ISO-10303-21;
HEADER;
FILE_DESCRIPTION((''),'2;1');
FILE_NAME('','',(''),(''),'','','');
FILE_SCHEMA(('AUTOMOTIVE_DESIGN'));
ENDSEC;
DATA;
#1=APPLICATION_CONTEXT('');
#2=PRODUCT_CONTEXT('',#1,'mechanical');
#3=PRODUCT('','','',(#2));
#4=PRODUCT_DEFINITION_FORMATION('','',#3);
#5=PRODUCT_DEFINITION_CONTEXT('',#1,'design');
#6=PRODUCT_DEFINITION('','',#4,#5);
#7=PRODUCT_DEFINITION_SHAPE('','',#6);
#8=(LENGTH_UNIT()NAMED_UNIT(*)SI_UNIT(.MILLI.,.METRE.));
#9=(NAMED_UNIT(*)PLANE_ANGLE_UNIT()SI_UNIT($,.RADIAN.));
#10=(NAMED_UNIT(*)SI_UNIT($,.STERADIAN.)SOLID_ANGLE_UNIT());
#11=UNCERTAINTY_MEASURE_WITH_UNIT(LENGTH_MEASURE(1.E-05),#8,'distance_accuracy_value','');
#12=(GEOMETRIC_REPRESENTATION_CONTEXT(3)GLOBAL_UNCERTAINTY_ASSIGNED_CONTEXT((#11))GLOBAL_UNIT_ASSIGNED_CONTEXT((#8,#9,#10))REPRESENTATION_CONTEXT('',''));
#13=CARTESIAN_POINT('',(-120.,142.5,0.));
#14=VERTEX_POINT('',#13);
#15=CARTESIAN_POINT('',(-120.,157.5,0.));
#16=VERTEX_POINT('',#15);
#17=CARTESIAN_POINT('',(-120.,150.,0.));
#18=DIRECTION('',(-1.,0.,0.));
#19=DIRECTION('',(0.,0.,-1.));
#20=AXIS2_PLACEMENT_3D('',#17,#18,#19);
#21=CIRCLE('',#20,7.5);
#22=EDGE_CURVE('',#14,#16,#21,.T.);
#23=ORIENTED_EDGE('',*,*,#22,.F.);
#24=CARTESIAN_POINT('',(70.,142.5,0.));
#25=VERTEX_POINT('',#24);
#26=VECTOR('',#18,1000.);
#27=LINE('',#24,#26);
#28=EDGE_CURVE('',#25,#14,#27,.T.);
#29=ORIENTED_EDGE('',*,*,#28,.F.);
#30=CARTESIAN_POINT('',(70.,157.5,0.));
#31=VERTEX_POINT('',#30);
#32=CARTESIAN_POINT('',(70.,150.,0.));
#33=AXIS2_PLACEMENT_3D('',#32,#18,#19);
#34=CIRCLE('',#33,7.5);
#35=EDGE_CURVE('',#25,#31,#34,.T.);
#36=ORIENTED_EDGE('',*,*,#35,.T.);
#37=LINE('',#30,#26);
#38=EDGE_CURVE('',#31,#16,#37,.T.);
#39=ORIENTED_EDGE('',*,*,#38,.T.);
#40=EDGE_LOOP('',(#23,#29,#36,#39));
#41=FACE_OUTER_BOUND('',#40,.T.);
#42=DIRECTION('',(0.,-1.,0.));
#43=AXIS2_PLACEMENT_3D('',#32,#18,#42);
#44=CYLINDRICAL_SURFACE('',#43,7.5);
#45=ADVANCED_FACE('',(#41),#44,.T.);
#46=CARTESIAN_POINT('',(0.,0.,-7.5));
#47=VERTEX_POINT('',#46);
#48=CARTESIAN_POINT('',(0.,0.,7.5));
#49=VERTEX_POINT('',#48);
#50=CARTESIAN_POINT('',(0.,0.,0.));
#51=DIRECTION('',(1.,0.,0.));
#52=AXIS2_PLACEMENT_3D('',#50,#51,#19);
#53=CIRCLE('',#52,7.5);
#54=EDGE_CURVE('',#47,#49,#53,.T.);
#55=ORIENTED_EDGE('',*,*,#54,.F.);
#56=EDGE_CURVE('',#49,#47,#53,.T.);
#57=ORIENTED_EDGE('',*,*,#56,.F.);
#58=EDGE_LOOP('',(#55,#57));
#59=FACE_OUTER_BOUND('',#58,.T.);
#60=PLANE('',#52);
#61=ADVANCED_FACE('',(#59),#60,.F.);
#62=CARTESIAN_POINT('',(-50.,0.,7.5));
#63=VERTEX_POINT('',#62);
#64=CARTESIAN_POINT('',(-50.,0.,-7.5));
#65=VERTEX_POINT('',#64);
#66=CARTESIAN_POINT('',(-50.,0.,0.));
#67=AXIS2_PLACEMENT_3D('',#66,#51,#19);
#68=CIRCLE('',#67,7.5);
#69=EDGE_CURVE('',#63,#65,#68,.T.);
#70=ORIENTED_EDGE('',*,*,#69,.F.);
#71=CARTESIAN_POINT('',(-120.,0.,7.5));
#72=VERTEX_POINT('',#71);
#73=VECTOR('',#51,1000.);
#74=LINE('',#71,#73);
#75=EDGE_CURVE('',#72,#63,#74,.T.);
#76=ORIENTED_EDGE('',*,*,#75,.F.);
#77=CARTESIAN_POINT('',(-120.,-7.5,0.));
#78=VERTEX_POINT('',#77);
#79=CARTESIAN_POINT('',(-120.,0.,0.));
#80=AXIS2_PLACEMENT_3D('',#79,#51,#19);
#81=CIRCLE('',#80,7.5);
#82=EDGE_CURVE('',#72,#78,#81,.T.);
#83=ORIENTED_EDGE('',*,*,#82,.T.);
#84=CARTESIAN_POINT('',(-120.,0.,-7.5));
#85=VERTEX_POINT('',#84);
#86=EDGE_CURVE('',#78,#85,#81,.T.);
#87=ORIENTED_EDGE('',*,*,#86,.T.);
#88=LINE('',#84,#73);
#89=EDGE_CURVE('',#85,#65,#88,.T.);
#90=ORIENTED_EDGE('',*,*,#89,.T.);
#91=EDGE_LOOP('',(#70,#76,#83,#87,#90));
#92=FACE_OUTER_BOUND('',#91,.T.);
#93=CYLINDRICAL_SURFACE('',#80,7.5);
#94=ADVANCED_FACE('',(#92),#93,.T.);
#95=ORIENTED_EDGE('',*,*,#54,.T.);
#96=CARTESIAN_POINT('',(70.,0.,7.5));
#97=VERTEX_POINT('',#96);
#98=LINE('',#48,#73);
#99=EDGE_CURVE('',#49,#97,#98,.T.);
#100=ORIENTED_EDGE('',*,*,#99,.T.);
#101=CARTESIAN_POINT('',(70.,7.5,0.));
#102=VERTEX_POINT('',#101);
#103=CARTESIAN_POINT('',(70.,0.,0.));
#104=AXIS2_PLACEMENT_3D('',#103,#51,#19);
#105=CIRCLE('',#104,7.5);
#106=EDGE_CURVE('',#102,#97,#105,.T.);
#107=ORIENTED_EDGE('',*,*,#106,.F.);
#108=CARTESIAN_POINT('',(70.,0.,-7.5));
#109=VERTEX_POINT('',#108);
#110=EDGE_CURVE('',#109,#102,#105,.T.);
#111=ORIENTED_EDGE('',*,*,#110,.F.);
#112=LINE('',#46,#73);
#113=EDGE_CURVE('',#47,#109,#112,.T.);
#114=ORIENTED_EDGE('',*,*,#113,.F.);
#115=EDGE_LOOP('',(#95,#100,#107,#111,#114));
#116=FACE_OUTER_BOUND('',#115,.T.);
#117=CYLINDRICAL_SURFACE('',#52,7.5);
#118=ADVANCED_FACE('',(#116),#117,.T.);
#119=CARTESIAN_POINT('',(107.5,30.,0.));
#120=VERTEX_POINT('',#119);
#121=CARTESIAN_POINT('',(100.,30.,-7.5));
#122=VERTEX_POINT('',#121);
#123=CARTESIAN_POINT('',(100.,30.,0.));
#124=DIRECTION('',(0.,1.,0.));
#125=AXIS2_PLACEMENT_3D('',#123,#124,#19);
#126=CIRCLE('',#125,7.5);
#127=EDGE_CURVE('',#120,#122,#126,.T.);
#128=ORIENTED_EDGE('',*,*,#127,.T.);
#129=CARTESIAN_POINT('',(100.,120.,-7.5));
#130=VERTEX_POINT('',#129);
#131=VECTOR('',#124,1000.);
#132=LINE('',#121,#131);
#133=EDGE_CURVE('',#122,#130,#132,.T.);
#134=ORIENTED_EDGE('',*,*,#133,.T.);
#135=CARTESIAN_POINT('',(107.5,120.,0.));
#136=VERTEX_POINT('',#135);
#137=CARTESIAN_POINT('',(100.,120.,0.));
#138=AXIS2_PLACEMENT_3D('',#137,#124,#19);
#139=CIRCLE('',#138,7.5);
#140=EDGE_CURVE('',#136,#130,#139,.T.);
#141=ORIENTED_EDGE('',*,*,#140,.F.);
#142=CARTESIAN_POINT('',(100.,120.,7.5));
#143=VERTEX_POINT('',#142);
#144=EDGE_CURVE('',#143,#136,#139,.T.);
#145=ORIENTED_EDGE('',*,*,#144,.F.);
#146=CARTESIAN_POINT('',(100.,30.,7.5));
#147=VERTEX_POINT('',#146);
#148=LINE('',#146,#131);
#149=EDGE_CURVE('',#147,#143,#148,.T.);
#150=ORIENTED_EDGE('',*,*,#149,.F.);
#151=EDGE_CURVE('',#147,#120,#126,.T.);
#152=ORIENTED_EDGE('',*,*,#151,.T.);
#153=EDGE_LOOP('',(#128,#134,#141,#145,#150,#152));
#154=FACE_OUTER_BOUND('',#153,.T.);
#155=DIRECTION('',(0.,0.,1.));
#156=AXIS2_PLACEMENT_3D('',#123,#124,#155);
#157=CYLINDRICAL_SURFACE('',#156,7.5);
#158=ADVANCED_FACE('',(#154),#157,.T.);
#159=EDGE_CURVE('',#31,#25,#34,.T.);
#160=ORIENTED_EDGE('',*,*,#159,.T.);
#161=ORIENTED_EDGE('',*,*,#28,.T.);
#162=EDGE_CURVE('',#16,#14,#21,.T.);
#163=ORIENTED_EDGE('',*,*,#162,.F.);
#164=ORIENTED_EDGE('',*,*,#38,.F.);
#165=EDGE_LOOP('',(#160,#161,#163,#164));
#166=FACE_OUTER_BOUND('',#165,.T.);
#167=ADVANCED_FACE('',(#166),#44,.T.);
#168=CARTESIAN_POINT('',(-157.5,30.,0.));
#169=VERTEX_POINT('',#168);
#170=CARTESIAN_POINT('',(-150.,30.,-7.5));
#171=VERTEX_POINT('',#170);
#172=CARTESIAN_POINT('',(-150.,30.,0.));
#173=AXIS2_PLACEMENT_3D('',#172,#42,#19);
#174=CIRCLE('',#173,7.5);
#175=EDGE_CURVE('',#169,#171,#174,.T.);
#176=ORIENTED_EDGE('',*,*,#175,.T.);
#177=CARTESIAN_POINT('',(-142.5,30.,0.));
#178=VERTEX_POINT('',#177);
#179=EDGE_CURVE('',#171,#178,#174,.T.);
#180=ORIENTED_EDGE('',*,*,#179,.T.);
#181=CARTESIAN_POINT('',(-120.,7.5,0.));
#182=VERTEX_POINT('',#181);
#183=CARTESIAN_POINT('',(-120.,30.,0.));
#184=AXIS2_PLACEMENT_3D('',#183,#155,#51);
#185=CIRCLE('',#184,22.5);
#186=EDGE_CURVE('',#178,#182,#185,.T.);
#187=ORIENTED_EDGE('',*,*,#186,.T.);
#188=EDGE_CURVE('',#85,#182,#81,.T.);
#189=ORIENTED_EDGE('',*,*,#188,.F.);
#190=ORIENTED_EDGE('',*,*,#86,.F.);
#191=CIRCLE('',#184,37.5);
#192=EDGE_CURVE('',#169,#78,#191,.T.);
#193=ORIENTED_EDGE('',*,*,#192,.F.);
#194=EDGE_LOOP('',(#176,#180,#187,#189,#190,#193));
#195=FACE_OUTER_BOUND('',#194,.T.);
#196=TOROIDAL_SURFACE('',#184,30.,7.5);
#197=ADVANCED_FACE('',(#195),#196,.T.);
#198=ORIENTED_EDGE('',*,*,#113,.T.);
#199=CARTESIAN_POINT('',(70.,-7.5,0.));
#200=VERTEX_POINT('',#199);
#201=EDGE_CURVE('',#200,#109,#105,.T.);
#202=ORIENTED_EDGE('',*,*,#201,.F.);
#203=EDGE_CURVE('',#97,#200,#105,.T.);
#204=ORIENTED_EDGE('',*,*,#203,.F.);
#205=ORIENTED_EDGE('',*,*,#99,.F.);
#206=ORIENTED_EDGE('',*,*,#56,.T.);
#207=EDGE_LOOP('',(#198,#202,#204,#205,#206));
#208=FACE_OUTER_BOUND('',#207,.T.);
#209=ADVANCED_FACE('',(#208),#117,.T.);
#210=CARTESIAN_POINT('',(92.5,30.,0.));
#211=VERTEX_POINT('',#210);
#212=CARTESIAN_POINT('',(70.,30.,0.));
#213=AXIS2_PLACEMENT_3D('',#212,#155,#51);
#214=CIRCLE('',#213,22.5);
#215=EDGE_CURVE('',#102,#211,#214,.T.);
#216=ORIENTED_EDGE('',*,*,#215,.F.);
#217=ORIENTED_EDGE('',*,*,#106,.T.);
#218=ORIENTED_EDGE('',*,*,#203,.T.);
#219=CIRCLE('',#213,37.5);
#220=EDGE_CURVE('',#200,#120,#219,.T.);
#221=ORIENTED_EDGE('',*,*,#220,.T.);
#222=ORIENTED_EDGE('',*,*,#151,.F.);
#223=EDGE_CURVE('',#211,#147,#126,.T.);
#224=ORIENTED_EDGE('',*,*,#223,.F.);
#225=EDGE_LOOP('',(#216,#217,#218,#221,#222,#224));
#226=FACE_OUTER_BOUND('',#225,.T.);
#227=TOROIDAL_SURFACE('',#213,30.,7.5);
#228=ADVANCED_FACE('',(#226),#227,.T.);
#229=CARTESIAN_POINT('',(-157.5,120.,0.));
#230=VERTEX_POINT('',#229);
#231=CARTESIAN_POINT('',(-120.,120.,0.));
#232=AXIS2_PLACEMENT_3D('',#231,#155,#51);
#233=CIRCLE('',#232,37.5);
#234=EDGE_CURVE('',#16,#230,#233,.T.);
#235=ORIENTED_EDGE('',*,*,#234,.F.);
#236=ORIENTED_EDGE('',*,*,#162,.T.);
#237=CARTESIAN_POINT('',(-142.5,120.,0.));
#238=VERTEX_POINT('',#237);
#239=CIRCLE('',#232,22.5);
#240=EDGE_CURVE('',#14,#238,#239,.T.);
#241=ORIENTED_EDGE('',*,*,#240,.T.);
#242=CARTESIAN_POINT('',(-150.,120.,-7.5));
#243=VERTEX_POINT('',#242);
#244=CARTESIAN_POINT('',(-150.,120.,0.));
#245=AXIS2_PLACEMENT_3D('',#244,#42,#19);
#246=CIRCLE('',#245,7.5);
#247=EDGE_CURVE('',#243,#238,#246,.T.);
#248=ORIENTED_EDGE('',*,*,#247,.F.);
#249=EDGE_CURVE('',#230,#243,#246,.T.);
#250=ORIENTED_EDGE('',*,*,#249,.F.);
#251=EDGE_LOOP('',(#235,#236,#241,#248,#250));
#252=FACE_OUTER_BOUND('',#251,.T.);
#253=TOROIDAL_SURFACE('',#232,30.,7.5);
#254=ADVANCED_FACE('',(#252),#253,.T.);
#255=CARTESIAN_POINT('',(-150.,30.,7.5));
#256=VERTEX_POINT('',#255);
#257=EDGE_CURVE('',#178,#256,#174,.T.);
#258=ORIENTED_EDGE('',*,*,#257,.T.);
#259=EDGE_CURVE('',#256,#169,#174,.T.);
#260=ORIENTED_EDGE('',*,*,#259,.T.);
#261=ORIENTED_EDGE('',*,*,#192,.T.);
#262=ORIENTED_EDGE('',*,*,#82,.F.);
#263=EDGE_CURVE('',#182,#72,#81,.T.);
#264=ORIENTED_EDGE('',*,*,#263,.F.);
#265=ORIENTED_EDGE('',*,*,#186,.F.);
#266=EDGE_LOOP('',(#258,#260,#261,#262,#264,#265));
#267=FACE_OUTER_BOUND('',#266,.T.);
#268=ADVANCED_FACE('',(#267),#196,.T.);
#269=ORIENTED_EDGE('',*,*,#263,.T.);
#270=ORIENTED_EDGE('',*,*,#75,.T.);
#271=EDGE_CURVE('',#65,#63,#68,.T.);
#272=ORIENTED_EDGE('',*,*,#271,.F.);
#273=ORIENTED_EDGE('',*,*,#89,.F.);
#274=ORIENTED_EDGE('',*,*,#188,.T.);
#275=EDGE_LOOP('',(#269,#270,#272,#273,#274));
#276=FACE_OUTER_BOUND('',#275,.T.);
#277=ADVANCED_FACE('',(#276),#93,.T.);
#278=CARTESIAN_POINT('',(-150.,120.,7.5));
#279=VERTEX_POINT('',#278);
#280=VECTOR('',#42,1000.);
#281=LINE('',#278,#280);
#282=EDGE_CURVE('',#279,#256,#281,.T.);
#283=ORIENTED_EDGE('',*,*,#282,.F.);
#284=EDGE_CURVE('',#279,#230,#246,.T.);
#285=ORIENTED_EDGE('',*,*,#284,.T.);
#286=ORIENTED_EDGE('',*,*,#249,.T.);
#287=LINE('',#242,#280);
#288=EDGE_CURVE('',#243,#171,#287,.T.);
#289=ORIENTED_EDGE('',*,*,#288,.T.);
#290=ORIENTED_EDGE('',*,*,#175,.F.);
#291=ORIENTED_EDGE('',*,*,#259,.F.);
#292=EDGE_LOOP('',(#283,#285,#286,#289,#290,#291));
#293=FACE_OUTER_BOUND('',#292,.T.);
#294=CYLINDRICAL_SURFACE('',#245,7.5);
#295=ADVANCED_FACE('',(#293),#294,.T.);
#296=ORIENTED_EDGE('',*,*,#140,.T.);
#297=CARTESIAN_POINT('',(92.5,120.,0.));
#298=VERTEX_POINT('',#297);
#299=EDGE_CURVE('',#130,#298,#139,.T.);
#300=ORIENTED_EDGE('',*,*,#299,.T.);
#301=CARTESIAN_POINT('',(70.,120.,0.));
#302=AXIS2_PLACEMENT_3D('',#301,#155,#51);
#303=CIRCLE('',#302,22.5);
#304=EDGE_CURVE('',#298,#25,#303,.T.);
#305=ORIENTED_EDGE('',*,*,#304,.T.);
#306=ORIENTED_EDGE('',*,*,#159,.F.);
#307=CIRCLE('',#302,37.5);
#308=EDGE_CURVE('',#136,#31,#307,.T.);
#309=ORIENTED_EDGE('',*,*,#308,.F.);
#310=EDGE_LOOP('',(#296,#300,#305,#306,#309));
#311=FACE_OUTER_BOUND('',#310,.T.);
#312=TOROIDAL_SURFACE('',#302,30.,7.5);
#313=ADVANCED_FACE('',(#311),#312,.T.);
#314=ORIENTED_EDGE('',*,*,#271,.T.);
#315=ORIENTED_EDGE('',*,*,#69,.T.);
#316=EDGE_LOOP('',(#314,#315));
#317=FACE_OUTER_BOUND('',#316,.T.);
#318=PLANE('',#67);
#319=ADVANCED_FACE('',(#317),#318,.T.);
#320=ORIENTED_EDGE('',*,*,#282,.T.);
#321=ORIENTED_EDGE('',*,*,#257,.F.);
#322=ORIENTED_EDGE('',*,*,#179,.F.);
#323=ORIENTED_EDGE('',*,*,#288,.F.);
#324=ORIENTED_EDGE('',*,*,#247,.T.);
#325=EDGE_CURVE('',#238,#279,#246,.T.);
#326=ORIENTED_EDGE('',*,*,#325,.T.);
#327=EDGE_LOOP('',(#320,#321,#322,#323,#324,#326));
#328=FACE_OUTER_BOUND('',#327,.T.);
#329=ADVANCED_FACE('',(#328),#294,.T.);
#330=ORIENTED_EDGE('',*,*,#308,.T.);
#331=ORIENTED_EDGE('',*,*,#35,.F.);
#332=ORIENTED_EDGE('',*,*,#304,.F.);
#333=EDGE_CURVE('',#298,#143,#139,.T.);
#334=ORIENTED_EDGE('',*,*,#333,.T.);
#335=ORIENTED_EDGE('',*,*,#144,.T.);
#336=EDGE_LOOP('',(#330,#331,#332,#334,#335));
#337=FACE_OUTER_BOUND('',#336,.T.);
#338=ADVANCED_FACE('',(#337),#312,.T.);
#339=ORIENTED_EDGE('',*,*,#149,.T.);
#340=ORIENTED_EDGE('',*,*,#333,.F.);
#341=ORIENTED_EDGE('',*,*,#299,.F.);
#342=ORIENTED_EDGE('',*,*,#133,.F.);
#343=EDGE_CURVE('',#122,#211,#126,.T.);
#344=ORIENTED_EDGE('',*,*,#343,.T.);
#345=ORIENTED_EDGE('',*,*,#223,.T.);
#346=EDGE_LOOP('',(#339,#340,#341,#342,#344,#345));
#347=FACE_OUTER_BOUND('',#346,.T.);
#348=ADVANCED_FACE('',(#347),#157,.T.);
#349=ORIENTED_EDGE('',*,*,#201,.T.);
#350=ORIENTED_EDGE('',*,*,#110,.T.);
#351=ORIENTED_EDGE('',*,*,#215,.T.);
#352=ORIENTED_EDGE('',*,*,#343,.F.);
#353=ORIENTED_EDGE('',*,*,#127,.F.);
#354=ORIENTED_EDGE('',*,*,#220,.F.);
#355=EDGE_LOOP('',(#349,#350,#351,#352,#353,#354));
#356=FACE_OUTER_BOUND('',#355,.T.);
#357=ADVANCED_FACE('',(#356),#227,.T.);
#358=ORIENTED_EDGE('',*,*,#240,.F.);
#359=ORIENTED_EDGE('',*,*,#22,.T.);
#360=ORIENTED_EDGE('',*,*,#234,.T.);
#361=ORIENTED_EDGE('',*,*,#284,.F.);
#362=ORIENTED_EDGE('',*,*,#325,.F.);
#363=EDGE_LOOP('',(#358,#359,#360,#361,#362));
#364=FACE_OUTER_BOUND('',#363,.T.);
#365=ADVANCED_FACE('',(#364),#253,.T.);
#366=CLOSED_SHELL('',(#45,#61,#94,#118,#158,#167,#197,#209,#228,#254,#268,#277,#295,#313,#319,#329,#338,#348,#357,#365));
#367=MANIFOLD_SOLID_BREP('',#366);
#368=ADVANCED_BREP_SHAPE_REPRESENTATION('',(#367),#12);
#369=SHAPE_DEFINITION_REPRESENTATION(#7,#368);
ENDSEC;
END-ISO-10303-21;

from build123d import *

# Parameters (mm, degrees)
SKETCH2_R = 7.5


with BuildPart() as part:
    # Sweep1: sweep along a path in Sketch1
    with BuildLine(Plane.XY) as sweep1_path:
        Line((0, 0), (70, 0))
        ThreePointArc((70, 0), (91.213203436, 8.786796564), (100, 30))
        Line((100, 30), (100, 120))
        ThreePointArc((100, 120), (91.213203436, 141.213203436), (70, 150))
        Line((70, 150), (-120, 150))
        ThreePointArc((-120, 150), (-141.213203436, 141.213203436), (-150, 120))
        Line((-150, 120), (-150, 30))
        ThreePointArc((-150, 30), (-141.213203436, 8.786796564), (-120, 0))
        Line((-120, 0), (-50, 0))
    # Sketch2 → Sweep1 (sweep)
    with BuildSketch(Plane(origin=(0, 0, 0), x_dir=(0, 0, -1), z_dir=(1, 0, 0))):
        Circle(SKETCH2_R)
    sweep(path=sweep1_path.line)


solid = part.part
